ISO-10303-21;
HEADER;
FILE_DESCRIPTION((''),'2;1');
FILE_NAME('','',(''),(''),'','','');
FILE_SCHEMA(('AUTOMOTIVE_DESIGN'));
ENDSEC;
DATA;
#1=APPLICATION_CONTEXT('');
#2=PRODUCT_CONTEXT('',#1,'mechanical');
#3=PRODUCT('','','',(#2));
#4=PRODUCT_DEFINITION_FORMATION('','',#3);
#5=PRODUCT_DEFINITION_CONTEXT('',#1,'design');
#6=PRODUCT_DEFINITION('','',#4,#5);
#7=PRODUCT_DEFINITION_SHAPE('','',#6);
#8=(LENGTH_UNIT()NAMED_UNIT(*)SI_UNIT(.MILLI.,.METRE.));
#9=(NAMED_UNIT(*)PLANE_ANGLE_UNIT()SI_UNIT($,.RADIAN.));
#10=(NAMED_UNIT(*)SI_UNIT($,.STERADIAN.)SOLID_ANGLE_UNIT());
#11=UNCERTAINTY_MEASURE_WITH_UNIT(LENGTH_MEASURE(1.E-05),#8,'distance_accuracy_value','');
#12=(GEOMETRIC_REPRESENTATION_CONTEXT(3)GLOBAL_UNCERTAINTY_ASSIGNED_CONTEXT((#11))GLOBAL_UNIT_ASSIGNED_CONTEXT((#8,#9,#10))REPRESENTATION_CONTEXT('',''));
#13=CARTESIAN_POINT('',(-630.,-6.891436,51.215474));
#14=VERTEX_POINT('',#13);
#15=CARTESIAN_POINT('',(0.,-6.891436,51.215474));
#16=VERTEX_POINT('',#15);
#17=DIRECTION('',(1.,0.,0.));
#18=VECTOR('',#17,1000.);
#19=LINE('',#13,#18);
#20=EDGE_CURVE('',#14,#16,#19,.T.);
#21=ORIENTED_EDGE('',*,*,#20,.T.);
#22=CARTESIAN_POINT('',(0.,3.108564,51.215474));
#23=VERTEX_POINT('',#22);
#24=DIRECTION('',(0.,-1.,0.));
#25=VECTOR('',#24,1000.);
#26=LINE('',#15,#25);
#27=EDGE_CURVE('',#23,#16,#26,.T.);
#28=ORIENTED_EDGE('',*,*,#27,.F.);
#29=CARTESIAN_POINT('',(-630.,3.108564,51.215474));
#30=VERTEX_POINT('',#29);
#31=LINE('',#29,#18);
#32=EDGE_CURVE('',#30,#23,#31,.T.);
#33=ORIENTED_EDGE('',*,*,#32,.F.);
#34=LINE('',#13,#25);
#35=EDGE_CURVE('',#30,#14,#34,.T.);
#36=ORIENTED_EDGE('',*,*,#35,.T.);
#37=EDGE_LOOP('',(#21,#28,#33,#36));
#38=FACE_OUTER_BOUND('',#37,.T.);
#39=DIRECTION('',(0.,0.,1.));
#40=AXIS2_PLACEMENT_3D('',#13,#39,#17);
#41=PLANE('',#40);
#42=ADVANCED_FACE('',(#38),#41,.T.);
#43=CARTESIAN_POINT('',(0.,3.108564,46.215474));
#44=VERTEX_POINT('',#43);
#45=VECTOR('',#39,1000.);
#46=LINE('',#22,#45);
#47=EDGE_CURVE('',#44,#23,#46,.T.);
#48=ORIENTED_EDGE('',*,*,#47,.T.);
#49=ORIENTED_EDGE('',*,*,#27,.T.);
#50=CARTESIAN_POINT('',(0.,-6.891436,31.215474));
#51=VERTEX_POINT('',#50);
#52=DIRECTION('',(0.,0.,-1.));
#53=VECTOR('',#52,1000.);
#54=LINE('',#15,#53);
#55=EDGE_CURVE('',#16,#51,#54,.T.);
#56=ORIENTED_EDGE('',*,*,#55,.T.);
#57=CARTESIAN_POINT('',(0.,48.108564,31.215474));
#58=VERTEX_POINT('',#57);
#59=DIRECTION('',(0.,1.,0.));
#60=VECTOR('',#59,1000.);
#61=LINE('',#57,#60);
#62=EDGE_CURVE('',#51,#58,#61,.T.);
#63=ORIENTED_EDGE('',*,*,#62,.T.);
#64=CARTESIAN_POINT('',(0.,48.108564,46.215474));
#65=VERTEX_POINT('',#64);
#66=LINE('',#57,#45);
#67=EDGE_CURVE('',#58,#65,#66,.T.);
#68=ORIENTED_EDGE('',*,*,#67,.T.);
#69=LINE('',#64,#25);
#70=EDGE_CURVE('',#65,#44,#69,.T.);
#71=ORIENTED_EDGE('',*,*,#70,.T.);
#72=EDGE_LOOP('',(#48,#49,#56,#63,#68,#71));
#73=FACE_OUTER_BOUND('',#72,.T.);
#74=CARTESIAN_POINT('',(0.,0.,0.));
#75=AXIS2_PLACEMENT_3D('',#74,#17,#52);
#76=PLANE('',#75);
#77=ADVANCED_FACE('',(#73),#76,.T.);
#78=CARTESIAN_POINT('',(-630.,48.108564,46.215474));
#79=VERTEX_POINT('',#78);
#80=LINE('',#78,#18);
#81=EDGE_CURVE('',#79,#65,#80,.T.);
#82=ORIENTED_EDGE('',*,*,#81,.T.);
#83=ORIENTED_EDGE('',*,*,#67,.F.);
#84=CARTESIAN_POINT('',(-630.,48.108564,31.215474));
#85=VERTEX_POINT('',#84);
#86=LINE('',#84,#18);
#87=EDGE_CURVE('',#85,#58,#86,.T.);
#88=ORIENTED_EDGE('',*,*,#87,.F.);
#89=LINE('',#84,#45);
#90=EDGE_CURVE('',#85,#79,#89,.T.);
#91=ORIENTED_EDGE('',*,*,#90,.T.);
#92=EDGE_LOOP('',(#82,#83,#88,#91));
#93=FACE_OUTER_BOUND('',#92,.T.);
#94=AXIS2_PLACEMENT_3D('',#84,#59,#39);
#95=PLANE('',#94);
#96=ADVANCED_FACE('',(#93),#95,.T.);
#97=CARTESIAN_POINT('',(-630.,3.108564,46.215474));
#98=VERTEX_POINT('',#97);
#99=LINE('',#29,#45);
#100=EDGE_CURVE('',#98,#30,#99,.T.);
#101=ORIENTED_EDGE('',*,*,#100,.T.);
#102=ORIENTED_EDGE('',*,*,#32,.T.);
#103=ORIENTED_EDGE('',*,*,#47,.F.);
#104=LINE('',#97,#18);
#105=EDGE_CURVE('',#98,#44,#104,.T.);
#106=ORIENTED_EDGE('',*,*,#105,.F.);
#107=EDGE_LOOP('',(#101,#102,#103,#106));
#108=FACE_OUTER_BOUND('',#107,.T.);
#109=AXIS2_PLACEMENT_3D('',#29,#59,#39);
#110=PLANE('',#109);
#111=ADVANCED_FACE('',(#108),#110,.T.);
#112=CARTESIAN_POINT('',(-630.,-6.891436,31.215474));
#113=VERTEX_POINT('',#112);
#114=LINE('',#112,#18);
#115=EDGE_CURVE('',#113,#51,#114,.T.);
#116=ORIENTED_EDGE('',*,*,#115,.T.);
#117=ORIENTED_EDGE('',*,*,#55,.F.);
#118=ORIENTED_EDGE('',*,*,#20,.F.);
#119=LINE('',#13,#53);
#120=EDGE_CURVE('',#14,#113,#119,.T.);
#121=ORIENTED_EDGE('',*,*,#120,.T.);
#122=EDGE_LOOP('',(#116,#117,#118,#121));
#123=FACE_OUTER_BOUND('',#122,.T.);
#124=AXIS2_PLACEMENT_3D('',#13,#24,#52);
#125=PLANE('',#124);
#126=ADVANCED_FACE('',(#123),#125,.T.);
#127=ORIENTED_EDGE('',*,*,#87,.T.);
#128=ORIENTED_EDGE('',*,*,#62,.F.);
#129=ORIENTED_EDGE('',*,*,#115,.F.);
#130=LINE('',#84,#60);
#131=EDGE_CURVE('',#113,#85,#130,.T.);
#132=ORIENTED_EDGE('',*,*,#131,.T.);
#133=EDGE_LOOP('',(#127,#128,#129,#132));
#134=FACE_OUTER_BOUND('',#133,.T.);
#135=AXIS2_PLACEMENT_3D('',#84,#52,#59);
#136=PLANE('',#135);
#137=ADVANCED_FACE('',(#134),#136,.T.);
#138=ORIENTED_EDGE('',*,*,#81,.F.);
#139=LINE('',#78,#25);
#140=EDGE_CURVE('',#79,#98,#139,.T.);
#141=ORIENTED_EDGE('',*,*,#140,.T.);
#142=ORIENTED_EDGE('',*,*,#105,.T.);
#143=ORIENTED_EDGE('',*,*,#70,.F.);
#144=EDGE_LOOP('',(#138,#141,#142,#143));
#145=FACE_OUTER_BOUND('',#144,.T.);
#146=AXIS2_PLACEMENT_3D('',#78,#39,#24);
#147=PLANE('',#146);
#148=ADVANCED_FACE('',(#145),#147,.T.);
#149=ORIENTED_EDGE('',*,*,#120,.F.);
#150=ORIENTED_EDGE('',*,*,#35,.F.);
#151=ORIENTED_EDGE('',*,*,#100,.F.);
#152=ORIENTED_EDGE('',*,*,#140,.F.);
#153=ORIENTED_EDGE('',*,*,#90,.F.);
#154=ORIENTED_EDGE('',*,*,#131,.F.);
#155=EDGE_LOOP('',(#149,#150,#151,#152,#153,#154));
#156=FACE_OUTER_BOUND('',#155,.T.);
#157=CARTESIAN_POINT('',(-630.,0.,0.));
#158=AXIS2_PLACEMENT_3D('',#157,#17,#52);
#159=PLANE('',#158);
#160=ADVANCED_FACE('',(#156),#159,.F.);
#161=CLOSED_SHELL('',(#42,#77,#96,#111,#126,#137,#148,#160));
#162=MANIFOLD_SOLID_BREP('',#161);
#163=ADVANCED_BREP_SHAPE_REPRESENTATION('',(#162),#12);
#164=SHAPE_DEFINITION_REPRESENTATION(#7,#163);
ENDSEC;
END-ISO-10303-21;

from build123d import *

# Parameters (mm, degrees)
BOSS_EXTRUDE1_DEPTH = 630


with BuildPart() as part:
    # Sketch1 → Boss-Extrude1 (new body)
    with BuildSketch(Plane(origin=(0, 0, 0), x_dir=(0, 0, -1), z_dir=(1, 0, 0))):
        Polygon((-31.215474357, 48.108563949), (-31.215474357, -6.891436051), (-51.215474357, -6.891436051), (-51.215474357, 3.108563949), (-46.215474357, 3.108563949), (-46.215474357, 48.108563949), align=None)
    extrude(amount=-BOSS_EXTRUDE1_DEPTH)


solid = part.part
